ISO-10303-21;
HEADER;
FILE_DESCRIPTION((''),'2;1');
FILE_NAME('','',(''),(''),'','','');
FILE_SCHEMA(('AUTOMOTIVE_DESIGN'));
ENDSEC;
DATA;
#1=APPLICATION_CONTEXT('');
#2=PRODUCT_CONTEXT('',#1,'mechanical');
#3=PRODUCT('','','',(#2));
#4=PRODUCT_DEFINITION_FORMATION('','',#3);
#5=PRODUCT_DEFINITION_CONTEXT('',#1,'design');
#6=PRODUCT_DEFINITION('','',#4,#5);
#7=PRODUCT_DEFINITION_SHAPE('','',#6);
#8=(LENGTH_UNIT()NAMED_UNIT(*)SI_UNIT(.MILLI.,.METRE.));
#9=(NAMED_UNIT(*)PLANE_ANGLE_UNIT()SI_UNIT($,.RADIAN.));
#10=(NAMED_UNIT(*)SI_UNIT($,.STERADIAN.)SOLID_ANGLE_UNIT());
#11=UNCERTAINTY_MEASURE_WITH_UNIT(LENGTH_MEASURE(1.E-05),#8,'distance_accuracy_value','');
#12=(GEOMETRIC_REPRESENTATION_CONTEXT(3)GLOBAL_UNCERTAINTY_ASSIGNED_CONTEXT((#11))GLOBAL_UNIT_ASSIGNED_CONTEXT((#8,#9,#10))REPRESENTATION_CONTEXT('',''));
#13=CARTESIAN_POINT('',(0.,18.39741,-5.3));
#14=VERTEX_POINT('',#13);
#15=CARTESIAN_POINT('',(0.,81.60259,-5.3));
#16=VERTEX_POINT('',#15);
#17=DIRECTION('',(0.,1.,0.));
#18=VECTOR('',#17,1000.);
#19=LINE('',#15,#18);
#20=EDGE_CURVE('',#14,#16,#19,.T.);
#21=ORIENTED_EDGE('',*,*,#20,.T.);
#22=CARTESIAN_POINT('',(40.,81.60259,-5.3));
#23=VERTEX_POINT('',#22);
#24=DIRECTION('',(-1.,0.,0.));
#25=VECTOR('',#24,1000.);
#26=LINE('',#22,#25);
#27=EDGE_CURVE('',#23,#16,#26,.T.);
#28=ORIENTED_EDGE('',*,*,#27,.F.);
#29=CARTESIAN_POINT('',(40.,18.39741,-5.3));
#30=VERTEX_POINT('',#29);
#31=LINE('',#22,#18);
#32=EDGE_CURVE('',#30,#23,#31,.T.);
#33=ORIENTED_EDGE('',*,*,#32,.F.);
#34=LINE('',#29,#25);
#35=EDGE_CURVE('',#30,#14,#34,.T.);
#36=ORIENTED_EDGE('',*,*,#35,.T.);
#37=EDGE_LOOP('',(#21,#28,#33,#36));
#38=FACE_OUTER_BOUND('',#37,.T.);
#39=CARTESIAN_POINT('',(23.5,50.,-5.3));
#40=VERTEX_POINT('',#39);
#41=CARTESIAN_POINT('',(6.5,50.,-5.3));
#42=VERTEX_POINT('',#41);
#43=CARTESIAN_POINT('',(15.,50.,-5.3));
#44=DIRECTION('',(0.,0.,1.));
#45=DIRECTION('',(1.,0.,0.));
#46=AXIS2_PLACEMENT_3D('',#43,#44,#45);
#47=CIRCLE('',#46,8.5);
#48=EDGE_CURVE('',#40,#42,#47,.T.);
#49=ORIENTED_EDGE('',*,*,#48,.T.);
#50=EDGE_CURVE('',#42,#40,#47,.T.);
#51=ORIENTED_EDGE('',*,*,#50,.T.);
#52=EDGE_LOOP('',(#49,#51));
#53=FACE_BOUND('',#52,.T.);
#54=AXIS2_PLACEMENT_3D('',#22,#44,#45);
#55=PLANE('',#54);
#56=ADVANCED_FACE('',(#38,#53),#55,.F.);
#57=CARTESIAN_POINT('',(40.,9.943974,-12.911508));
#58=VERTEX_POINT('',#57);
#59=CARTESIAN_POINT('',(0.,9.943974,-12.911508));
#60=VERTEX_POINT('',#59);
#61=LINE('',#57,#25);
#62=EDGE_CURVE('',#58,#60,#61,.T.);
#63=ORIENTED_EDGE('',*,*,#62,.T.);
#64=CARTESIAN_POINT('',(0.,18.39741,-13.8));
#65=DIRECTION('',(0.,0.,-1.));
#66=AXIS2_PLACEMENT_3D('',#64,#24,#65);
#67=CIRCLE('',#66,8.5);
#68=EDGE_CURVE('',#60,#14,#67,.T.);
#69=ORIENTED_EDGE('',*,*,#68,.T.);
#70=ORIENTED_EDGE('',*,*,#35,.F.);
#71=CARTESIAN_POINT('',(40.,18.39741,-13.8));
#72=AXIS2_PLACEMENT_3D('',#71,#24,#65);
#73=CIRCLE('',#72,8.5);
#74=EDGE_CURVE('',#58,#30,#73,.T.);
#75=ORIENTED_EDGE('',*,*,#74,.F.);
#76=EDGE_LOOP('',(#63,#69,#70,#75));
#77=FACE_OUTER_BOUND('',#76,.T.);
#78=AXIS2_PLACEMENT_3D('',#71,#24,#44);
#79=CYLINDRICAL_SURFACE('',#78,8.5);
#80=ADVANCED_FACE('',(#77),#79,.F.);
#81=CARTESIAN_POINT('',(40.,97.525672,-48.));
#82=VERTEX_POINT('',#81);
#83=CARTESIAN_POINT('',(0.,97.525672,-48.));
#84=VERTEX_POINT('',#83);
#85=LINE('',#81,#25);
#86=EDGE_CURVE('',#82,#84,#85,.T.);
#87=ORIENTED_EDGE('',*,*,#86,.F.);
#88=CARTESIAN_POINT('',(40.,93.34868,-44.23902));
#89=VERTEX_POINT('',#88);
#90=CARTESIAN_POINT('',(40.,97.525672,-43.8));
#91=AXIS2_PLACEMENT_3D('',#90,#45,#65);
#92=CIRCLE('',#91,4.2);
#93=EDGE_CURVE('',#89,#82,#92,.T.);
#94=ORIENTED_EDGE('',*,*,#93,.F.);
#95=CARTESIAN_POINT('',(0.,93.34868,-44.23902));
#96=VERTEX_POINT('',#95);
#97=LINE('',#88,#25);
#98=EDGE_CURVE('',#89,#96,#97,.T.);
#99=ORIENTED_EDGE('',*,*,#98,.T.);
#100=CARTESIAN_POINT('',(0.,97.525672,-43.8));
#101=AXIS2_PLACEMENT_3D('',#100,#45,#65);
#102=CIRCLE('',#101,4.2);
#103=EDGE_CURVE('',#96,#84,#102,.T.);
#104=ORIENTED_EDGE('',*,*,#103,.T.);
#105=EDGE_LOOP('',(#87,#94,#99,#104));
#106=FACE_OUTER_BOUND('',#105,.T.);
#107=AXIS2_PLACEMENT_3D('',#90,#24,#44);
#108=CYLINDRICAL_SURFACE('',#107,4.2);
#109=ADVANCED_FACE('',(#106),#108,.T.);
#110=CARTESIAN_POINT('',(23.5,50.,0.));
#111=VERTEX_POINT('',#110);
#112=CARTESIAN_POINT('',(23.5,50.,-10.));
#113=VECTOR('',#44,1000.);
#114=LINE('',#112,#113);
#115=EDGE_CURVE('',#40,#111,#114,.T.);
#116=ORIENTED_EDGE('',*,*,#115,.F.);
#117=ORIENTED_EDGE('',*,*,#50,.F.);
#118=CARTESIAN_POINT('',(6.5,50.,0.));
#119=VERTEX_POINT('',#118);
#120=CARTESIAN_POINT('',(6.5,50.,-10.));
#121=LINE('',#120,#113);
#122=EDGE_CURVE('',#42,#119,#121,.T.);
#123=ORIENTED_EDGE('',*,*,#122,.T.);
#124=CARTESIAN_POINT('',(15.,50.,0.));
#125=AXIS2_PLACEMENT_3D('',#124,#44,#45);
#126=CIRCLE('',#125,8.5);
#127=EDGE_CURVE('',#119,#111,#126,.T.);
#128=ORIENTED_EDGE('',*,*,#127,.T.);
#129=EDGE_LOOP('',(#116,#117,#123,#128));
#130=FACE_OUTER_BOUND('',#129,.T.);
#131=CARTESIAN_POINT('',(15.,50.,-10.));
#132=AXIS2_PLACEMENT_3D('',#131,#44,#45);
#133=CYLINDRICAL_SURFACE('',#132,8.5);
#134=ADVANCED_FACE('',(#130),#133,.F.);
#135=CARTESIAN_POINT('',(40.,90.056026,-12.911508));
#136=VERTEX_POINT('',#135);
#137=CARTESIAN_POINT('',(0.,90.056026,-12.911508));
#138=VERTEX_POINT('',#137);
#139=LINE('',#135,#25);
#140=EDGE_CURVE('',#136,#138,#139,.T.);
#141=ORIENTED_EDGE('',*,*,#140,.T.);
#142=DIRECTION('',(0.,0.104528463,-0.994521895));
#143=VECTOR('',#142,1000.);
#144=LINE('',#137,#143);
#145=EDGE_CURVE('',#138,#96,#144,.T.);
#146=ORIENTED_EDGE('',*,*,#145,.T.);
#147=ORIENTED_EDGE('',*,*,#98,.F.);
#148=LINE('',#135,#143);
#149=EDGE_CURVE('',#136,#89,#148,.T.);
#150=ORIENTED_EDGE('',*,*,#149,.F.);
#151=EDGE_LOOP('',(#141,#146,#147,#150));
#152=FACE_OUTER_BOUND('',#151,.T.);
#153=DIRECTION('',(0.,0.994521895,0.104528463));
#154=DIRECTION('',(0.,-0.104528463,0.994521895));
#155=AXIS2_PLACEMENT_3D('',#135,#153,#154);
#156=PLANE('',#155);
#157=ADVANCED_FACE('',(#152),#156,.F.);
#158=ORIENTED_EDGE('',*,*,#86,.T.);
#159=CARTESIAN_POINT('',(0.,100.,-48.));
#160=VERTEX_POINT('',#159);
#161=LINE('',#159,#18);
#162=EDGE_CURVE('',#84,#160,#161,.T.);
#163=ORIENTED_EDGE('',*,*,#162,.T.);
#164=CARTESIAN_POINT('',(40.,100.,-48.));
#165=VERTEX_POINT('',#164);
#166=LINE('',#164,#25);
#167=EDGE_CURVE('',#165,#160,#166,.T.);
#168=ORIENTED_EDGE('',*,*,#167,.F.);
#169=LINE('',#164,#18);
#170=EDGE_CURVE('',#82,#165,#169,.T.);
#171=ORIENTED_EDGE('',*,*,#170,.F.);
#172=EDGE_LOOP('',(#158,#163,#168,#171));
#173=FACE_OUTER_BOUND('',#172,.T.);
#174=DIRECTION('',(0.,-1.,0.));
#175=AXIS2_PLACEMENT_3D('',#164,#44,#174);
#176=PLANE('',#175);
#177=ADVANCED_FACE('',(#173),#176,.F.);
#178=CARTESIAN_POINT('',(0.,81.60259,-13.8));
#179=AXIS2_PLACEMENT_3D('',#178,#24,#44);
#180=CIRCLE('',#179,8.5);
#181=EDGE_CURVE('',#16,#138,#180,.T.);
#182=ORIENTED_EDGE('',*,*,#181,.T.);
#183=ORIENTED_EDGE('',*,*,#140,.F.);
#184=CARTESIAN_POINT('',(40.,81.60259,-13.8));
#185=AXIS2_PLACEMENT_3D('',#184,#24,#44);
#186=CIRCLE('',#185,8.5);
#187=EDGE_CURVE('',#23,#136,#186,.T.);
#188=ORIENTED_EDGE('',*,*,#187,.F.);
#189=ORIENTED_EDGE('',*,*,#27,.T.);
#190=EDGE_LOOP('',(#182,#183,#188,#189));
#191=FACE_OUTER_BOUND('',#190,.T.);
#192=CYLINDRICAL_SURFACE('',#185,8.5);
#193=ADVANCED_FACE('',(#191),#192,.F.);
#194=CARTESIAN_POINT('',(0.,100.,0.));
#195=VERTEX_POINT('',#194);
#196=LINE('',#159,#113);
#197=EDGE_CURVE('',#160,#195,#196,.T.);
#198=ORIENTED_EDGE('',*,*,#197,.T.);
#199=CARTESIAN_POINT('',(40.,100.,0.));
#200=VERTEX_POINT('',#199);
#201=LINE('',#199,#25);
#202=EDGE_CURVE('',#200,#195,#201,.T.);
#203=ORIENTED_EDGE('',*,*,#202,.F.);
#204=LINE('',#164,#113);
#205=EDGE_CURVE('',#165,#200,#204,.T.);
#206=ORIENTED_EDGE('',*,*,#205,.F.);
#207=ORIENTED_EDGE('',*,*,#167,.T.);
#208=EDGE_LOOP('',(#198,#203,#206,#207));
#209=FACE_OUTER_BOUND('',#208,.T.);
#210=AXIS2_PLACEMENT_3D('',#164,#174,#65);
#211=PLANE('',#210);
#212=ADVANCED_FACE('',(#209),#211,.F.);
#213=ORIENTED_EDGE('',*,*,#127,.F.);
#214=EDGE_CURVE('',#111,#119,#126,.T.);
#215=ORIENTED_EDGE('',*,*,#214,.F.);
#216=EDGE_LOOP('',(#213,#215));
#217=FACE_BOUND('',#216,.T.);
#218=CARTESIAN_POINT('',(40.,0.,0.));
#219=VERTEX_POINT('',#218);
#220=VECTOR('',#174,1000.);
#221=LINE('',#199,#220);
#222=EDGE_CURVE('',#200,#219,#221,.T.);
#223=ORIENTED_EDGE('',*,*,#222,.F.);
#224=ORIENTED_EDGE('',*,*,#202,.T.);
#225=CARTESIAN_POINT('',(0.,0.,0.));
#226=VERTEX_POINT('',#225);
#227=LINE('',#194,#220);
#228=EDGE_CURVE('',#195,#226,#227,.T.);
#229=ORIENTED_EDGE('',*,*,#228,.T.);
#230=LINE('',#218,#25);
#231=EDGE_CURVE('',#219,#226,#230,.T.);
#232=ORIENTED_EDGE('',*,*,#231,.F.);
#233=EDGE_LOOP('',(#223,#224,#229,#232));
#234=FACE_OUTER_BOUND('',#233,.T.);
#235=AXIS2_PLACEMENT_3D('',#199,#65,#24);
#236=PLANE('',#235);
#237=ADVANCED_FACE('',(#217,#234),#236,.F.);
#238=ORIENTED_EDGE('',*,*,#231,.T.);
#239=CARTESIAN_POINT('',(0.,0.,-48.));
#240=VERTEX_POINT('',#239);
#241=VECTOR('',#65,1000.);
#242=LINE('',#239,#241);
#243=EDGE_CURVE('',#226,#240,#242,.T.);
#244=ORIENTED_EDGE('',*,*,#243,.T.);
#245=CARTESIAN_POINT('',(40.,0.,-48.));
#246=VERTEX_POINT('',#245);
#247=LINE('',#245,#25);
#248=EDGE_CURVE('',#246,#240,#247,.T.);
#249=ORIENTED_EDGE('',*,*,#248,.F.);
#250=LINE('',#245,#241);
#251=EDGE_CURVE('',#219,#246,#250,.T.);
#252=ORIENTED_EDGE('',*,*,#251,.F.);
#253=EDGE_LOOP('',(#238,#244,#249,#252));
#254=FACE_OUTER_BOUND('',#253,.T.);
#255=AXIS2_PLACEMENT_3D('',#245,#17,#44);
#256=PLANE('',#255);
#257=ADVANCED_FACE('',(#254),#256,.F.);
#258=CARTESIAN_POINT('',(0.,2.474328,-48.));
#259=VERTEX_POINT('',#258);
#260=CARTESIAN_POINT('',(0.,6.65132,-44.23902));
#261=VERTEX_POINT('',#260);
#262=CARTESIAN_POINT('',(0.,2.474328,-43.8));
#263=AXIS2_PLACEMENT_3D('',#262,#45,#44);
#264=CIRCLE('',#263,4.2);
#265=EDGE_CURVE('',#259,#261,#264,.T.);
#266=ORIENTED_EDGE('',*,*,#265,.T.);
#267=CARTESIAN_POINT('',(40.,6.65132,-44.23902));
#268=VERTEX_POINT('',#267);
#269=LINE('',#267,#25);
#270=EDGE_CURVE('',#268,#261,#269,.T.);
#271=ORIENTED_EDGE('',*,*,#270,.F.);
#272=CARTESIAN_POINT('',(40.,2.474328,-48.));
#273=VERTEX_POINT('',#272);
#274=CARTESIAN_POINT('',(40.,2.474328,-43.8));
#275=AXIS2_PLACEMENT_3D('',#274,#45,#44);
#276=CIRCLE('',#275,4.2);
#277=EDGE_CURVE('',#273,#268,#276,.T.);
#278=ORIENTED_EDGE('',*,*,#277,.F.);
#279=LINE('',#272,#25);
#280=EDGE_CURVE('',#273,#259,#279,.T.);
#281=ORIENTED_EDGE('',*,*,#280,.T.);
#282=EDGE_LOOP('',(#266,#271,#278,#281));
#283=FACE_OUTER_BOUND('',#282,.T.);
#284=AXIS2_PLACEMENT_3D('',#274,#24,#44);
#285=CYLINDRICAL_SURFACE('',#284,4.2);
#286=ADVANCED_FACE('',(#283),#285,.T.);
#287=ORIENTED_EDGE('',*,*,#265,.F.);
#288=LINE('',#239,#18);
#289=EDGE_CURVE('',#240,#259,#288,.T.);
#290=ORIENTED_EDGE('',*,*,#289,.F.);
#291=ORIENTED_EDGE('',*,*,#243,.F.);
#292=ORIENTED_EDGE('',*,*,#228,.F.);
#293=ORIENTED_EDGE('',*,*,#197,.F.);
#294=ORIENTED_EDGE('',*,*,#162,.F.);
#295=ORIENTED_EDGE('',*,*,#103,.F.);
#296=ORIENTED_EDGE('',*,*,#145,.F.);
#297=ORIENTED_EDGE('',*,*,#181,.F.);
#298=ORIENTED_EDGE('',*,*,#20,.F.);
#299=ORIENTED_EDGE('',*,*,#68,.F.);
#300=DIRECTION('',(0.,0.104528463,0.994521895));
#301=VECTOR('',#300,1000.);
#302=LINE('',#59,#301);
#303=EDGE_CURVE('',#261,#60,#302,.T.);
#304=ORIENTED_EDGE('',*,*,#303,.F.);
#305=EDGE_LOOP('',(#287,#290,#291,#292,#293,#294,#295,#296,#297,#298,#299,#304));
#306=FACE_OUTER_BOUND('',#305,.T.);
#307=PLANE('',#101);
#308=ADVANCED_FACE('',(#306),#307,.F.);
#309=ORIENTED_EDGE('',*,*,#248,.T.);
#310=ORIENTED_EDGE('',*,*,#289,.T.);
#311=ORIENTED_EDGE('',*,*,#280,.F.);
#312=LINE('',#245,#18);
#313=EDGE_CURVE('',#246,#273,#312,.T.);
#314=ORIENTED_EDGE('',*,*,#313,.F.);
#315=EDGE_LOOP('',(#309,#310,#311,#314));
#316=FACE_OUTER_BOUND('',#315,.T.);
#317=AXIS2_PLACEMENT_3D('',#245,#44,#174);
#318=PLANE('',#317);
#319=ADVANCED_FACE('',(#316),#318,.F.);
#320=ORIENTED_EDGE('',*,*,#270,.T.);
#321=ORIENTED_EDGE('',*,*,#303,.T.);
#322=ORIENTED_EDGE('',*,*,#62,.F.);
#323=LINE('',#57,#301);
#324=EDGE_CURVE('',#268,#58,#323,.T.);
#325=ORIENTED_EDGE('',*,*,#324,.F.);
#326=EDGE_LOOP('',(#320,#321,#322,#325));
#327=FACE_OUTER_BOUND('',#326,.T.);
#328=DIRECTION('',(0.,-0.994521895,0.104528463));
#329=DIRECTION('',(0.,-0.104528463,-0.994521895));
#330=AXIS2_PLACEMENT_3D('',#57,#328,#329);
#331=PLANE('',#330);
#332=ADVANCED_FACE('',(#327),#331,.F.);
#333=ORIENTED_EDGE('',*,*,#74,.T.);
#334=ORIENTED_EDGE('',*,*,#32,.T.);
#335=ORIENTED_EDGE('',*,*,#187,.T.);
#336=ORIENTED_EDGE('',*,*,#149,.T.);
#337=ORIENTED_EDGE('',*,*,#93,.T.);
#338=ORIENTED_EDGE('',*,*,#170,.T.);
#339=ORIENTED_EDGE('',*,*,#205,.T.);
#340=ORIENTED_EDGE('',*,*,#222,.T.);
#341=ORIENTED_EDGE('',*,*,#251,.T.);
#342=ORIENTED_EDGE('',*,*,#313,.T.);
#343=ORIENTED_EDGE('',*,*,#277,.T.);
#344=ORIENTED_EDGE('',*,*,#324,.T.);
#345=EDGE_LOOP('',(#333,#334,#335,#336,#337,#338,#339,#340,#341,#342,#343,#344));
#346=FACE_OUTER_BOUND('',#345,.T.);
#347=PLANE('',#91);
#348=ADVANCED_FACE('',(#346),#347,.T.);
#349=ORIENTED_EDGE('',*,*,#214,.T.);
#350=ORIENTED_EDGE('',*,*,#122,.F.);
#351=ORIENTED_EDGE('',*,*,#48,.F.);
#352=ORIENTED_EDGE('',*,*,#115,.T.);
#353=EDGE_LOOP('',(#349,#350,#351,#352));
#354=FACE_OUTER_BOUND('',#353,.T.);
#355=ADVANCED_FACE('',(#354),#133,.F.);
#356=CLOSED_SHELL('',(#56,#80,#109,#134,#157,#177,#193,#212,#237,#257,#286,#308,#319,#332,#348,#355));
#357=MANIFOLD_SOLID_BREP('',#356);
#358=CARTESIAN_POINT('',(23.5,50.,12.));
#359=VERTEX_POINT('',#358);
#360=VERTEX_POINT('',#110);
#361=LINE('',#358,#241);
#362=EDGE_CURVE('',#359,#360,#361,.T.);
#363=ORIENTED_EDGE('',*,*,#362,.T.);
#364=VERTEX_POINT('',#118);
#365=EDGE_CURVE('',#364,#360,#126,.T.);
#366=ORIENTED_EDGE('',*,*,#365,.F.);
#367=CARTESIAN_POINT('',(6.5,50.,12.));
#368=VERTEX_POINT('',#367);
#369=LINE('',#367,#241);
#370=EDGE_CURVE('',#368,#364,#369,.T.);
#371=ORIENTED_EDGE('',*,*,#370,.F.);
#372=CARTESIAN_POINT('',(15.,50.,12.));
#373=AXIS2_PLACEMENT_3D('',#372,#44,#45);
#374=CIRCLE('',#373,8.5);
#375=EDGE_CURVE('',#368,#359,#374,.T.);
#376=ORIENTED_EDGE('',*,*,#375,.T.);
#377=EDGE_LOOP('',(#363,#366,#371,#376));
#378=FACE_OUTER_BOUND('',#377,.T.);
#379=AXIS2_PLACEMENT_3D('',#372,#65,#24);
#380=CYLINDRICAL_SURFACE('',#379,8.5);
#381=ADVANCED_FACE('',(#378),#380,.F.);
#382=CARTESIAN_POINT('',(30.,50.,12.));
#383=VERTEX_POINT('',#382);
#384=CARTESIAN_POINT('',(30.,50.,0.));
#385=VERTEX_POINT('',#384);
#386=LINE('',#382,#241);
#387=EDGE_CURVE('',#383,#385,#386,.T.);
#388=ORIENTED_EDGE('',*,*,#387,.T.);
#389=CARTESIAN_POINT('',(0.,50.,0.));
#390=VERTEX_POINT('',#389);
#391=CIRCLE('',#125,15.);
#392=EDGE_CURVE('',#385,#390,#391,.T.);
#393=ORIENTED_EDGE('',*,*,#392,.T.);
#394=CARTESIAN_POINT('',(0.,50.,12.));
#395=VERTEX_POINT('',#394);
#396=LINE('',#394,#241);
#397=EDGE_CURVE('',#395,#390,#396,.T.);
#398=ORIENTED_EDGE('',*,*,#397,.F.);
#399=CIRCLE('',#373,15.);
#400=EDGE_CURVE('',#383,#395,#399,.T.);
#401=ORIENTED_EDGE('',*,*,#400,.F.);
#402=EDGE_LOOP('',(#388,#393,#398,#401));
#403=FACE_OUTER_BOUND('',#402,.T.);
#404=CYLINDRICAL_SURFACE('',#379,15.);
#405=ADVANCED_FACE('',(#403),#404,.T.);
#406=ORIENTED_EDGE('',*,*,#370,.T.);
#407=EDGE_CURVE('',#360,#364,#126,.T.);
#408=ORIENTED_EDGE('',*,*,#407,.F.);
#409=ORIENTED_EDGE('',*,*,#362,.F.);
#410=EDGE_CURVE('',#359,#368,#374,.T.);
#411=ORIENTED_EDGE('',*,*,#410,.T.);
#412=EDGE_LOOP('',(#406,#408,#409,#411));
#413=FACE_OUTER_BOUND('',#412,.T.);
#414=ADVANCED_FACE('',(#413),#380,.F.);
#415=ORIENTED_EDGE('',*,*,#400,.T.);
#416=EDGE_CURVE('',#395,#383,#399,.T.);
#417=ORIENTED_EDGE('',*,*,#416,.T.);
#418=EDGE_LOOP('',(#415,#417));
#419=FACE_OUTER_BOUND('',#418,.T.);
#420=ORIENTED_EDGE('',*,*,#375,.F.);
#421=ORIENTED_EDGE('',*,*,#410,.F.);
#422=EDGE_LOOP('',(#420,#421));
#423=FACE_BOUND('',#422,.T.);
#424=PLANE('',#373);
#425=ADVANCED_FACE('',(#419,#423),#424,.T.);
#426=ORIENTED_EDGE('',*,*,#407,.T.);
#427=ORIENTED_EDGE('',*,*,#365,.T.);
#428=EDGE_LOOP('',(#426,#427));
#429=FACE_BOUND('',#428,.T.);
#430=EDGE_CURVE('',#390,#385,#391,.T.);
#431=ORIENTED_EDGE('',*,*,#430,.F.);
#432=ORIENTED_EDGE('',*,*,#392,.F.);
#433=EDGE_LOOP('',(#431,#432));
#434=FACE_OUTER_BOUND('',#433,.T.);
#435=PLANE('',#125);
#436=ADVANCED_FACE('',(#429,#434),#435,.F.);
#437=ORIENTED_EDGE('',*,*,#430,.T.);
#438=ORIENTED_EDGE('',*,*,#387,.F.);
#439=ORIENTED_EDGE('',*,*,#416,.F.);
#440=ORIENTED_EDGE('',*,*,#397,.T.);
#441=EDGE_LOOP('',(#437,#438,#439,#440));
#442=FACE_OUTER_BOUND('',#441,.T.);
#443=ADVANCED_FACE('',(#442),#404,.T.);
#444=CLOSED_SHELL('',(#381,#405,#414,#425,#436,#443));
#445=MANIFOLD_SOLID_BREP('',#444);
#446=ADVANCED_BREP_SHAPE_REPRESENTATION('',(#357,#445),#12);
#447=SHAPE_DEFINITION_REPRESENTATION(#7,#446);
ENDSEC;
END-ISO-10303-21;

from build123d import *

# Parameters (mm, degrees)
HOT_ROLLED_CHANNEL_GB_T706_2008_10_1_DEPTH = 40
SKETCH2_R                                  = 8.5
CUT_EXTRUDE1_DEPTH                         = 10
SKETCH3_R                                  = 15
SKETCH3_R_2                                = 8.5
BOSS_EXTRUDE1_DEPTH                        = 12


with BuildPart() as part:
    # Sketch1 → Hot-rolled channel gb∕t706-2008 10(1) (new body)
    with BuildSketch(Plane(origin=(0, 0, 0), x_dir=(0, 0, -1), z_dir=(1, 0, 0))):
        with BuildLine():
            Line((48, 100), (0, 100))
            Line((0, 100), (0, 0))
            Line((0, 0), (48, 0))
            Line((48, 0), (48, 2.474327591))
            ThreePointArc((48, 2.474327591), (46.921208267, 5.284676138), (44.239019546, 6.651319552))
            Line((44.239019546, 6.651319552), (12.911508062, 9.943973689))
            ThreePointArc((12.911508062, 9.943973689), (7.483268983, 12.709799645), (5.3, 18.397409799))
            Line((5.3, 18.397409799), (5.3, 81.602590201))
            ThreePointArc((5.3, 81.602590201), (7.483268983, 87.290200355), (12.911508062, 90.056026311))
            Line((12.911508062, 90.056026311), (44.239019546, 93.348680448))
            ThreePointArc((44.239019546, 93.348680448), (46.921208267, 94.715323862), (48, 97.525672409))
            Line((48, 97.525672409), (48, 100))
        make_face()
    extrude(amount=HOT_ROLLED_CHANNEL_GB_T706_2008_10_1_DEPTH)

    # Sketch2 → Cut-Extrude1 (cut)
    with BuildSketch(Plane.XY):
        with Locations((15, 50)):
            Circle(SKETCH2_R)
    extrude(amount=-CUT_EXTRUDE1_DEPTH, mode=Mode.SUBTRACT)


with BuildPart() as body_2:
    # Sketch3 → Boss-Extrude1 (new body)
    with BuildSketch(Plane.XY):
        with Locations((15, 50)):
            Circle(SKETCH3_R)
        with Locations((15, 50)):
            Circle(SKETCH3_R_2, mode=Mode.SUBTRACT)
    extrude(amount=BOSS_EXTRUDE1_DEPTH)


solid = Compound([part.part, body_2.part])
